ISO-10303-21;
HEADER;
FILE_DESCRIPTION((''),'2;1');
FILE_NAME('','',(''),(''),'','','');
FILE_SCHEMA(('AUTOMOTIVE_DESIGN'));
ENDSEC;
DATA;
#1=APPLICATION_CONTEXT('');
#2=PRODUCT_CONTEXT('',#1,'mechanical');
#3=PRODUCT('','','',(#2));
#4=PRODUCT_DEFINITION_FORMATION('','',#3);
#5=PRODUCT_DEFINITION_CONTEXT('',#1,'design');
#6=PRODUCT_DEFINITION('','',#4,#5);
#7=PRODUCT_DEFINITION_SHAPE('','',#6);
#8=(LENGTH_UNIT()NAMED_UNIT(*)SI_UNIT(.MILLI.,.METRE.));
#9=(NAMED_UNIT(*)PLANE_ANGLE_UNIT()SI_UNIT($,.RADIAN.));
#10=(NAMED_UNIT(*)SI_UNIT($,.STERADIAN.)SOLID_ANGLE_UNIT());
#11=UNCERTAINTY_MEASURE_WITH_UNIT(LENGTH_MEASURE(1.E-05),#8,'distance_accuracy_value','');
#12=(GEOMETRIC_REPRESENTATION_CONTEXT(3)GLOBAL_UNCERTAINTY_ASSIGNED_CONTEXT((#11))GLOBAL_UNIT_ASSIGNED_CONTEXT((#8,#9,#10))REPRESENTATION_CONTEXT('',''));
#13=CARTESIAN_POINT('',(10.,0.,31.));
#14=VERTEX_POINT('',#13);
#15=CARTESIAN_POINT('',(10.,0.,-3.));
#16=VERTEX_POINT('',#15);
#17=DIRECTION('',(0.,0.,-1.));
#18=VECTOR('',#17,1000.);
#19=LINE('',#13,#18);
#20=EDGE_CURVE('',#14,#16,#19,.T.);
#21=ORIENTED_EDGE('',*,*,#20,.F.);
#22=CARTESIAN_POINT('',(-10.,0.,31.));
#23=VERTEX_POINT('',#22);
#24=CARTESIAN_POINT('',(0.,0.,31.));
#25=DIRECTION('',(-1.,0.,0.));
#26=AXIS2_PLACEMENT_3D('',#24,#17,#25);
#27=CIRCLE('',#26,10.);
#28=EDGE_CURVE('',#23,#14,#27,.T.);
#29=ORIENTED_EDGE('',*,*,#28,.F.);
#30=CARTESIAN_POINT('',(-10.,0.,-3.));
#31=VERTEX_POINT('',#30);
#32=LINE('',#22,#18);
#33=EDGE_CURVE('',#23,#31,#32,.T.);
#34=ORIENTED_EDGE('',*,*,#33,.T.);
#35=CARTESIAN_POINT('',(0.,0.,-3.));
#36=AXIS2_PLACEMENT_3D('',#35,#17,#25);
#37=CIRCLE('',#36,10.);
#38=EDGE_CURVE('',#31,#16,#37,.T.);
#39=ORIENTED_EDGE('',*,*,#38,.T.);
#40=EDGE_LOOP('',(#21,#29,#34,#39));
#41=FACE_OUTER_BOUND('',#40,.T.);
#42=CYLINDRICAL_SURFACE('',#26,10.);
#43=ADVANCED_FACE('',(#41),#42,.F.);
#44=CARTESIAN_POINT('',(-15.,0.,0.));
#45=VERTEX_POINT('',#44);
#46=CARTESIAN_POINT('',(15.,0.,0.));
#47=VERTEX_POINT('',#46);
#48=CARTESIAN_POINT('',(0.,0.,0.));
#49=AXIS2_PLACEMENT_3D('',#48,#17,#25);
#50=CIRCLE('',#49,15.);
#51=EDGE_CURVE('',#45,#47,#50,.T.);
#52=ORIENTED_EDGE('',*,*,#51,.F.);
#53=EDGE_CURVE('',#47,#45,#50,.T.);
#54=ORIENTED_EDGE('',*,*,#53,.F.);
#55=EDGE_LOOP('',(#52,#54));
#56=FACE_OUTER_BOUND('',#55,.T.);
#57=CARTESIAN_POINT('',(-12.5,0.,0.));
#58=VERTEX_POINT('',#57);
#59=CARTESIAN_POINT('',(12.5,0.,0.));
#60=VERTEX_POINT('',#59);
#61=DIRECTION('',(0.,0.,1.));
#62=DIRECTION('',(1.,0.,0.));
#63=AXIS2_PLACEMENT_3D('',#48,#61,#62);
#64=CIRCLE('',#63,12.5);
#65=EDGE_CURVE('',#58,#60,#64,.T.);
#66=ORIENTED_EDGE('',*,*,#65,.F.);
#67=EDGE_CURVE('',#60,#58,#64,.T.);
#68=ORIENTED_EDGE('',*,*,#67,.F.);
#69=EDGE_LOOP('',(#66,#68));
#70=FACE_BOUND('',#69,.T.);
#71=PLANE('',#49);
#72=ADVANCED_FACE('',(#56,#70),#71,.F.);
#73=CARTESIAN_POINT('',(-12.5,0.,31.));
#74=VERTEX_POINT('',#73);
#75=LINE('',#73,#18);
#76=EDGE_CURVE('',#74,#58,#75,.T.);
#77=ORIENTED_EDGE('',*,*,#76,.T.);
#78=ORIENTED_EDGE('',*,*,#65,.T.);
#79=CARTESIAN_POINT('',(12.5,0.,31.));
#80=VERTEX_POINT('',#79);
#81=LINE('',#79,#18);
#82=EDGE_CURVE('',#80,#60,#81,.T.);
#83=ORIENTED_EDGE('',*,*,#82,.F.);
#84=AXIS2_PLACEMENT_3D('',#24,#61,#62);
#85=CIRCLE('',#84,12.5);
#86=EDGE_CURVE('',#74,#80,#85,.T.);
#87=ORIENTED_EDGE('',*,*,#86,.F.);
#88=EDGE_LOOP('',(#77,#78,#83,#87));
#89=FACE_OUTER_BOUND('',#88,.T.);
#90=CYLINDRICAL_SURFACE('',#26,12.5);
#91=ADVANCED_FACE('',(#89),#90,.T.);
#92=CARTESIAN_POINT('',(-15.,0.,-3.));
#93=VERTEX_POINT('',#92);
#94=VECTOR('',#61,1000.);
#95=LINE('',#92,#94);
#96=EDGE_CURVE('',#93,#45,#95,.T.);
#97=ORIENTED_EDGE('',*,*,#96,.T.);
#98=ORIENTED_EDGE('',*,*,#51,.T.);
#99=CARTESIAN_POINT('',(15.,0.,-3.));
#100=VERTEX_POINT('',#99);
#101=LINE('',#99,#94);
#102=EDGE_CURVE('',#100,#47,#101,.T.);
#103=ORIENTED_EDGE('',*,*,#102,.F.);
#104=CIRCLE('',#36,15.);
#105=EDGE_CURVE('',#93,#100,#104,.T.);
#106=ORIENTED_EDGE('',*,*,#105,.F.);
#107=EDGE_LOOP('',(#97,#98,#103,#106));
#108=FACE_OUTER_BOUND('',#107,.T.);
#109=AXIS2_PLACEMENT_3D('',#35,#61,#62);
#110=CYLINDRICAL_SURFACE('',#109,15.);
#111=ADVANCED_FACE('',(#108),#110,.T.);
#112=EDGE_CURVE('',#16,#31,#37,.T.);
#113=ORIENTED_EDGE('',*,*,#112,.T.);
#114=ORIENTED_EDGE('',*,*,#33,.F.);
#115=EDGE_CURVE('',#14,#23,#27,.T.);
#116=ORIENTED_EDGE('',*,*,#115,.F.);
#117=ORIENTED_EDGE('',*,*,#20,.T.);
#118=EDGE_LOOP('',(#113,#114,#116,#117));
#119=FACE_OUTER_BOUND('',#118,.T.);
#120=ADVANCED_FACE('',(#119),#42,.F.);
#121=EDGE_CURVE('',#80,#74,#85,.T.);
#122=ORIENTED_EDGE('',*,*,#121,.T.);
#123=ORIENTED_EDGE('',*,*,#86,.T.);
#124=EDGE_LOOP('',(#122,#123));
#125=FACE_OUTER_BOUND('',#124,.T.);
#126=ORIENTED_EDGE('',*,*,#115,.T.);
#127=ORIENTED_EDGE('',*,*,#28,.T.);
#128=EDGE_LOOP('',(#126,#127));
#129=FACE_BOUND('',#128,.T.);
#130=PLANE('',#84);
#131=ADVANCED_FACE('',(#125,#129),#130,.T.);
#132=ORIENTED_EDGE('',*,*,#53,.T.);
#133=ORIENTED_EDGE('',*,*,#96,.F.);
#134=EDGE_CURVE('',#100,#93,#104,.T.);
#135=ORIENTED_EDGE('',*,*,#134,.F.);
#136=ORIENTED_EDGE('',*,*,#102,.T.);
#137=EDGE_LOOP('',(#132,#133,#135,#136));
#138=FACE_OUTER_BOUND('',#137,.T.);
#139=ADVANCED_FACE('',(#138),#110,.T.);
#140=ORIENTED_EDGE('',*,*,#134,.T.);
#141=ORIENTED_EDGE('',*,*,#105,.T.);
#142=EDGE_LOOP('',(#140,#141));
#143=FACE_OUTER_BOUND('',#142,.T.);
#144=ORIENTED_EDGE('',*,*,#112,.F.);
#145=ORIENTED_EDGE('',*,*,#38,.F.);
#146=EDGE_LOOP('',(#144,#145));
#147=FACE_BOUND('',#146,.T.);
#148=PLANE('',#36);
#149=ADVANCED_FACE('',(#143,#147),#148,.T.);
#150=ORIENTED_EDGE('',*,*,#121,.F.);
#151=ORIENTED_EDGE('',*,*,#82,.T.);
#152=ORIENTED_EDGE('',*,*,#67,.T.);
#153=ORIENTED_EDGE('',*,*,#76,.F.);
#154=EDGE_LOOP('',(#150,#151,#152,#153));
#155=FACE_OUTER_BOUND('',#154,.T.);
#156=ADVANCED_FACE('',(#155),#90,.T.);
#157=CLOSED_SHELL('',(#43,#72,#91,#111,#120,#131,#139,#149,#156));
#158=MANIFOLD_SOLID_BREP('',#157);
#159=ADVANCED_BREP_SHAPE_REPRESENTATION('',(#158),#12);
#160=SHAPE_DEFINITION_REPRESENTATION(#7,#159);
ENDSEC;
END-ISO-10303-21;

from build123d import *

# Parameters (mm, degrees)
BODY_PROFILE_25_R          = 12.5
BUSH_BODY_25X31_DEPTH      = 31
FLANGE_PROFILE_30_R        = 15
FLANGE_30X3_DEPTH          = 3
BORE_20_THROUGH_DEPTH      = 41.074929819
BORE_20_THROUGH_DEPTH_BACK = 41.074929819
BORE_PROFILE_20_R          = 10


with BuildPart() as part:
    # Body Profile Ø25 → Bush Body Ø25x31 (new body)
    with BuildSketch(Plane.XY):
        Circle(BODY_PROFILE_25_R)
    extrude(amount=BUSH_BODY_25X31_DEPTH)

    # Flange Profile Ø30 → Flange Ø30x3 (add)
    with BuildSketch(Plane(origin=(0, 0, 0), x_dir=(-1, 0, 0), z_dir=(0, 0, -1))):
        Circle(FLANGE_PROFILE_30_R)
    extrude(amount=FLANGE_30X3_DEPTH)

    # Bore Profile Ø20 → Bore Ø20 Through (cut, two sides: drawn at the far end of the back side and taken through both)
    with BuildSketch(Plane(origin=(0, 0, -3), x_dir=(-1, 0, 0), z_dir=(0, 0, -1)).offset(-BORE_20_THROUGH_DEPTH_BACK)):
        Circle(BORE_PROFILE_20_R)
    extrude(amount=BORE_20_THROUGH_DEPTH + BORE_20_THROUGH_DEPTH_BACK, mode=Mode.SUBTRACT)


solid = part.part
